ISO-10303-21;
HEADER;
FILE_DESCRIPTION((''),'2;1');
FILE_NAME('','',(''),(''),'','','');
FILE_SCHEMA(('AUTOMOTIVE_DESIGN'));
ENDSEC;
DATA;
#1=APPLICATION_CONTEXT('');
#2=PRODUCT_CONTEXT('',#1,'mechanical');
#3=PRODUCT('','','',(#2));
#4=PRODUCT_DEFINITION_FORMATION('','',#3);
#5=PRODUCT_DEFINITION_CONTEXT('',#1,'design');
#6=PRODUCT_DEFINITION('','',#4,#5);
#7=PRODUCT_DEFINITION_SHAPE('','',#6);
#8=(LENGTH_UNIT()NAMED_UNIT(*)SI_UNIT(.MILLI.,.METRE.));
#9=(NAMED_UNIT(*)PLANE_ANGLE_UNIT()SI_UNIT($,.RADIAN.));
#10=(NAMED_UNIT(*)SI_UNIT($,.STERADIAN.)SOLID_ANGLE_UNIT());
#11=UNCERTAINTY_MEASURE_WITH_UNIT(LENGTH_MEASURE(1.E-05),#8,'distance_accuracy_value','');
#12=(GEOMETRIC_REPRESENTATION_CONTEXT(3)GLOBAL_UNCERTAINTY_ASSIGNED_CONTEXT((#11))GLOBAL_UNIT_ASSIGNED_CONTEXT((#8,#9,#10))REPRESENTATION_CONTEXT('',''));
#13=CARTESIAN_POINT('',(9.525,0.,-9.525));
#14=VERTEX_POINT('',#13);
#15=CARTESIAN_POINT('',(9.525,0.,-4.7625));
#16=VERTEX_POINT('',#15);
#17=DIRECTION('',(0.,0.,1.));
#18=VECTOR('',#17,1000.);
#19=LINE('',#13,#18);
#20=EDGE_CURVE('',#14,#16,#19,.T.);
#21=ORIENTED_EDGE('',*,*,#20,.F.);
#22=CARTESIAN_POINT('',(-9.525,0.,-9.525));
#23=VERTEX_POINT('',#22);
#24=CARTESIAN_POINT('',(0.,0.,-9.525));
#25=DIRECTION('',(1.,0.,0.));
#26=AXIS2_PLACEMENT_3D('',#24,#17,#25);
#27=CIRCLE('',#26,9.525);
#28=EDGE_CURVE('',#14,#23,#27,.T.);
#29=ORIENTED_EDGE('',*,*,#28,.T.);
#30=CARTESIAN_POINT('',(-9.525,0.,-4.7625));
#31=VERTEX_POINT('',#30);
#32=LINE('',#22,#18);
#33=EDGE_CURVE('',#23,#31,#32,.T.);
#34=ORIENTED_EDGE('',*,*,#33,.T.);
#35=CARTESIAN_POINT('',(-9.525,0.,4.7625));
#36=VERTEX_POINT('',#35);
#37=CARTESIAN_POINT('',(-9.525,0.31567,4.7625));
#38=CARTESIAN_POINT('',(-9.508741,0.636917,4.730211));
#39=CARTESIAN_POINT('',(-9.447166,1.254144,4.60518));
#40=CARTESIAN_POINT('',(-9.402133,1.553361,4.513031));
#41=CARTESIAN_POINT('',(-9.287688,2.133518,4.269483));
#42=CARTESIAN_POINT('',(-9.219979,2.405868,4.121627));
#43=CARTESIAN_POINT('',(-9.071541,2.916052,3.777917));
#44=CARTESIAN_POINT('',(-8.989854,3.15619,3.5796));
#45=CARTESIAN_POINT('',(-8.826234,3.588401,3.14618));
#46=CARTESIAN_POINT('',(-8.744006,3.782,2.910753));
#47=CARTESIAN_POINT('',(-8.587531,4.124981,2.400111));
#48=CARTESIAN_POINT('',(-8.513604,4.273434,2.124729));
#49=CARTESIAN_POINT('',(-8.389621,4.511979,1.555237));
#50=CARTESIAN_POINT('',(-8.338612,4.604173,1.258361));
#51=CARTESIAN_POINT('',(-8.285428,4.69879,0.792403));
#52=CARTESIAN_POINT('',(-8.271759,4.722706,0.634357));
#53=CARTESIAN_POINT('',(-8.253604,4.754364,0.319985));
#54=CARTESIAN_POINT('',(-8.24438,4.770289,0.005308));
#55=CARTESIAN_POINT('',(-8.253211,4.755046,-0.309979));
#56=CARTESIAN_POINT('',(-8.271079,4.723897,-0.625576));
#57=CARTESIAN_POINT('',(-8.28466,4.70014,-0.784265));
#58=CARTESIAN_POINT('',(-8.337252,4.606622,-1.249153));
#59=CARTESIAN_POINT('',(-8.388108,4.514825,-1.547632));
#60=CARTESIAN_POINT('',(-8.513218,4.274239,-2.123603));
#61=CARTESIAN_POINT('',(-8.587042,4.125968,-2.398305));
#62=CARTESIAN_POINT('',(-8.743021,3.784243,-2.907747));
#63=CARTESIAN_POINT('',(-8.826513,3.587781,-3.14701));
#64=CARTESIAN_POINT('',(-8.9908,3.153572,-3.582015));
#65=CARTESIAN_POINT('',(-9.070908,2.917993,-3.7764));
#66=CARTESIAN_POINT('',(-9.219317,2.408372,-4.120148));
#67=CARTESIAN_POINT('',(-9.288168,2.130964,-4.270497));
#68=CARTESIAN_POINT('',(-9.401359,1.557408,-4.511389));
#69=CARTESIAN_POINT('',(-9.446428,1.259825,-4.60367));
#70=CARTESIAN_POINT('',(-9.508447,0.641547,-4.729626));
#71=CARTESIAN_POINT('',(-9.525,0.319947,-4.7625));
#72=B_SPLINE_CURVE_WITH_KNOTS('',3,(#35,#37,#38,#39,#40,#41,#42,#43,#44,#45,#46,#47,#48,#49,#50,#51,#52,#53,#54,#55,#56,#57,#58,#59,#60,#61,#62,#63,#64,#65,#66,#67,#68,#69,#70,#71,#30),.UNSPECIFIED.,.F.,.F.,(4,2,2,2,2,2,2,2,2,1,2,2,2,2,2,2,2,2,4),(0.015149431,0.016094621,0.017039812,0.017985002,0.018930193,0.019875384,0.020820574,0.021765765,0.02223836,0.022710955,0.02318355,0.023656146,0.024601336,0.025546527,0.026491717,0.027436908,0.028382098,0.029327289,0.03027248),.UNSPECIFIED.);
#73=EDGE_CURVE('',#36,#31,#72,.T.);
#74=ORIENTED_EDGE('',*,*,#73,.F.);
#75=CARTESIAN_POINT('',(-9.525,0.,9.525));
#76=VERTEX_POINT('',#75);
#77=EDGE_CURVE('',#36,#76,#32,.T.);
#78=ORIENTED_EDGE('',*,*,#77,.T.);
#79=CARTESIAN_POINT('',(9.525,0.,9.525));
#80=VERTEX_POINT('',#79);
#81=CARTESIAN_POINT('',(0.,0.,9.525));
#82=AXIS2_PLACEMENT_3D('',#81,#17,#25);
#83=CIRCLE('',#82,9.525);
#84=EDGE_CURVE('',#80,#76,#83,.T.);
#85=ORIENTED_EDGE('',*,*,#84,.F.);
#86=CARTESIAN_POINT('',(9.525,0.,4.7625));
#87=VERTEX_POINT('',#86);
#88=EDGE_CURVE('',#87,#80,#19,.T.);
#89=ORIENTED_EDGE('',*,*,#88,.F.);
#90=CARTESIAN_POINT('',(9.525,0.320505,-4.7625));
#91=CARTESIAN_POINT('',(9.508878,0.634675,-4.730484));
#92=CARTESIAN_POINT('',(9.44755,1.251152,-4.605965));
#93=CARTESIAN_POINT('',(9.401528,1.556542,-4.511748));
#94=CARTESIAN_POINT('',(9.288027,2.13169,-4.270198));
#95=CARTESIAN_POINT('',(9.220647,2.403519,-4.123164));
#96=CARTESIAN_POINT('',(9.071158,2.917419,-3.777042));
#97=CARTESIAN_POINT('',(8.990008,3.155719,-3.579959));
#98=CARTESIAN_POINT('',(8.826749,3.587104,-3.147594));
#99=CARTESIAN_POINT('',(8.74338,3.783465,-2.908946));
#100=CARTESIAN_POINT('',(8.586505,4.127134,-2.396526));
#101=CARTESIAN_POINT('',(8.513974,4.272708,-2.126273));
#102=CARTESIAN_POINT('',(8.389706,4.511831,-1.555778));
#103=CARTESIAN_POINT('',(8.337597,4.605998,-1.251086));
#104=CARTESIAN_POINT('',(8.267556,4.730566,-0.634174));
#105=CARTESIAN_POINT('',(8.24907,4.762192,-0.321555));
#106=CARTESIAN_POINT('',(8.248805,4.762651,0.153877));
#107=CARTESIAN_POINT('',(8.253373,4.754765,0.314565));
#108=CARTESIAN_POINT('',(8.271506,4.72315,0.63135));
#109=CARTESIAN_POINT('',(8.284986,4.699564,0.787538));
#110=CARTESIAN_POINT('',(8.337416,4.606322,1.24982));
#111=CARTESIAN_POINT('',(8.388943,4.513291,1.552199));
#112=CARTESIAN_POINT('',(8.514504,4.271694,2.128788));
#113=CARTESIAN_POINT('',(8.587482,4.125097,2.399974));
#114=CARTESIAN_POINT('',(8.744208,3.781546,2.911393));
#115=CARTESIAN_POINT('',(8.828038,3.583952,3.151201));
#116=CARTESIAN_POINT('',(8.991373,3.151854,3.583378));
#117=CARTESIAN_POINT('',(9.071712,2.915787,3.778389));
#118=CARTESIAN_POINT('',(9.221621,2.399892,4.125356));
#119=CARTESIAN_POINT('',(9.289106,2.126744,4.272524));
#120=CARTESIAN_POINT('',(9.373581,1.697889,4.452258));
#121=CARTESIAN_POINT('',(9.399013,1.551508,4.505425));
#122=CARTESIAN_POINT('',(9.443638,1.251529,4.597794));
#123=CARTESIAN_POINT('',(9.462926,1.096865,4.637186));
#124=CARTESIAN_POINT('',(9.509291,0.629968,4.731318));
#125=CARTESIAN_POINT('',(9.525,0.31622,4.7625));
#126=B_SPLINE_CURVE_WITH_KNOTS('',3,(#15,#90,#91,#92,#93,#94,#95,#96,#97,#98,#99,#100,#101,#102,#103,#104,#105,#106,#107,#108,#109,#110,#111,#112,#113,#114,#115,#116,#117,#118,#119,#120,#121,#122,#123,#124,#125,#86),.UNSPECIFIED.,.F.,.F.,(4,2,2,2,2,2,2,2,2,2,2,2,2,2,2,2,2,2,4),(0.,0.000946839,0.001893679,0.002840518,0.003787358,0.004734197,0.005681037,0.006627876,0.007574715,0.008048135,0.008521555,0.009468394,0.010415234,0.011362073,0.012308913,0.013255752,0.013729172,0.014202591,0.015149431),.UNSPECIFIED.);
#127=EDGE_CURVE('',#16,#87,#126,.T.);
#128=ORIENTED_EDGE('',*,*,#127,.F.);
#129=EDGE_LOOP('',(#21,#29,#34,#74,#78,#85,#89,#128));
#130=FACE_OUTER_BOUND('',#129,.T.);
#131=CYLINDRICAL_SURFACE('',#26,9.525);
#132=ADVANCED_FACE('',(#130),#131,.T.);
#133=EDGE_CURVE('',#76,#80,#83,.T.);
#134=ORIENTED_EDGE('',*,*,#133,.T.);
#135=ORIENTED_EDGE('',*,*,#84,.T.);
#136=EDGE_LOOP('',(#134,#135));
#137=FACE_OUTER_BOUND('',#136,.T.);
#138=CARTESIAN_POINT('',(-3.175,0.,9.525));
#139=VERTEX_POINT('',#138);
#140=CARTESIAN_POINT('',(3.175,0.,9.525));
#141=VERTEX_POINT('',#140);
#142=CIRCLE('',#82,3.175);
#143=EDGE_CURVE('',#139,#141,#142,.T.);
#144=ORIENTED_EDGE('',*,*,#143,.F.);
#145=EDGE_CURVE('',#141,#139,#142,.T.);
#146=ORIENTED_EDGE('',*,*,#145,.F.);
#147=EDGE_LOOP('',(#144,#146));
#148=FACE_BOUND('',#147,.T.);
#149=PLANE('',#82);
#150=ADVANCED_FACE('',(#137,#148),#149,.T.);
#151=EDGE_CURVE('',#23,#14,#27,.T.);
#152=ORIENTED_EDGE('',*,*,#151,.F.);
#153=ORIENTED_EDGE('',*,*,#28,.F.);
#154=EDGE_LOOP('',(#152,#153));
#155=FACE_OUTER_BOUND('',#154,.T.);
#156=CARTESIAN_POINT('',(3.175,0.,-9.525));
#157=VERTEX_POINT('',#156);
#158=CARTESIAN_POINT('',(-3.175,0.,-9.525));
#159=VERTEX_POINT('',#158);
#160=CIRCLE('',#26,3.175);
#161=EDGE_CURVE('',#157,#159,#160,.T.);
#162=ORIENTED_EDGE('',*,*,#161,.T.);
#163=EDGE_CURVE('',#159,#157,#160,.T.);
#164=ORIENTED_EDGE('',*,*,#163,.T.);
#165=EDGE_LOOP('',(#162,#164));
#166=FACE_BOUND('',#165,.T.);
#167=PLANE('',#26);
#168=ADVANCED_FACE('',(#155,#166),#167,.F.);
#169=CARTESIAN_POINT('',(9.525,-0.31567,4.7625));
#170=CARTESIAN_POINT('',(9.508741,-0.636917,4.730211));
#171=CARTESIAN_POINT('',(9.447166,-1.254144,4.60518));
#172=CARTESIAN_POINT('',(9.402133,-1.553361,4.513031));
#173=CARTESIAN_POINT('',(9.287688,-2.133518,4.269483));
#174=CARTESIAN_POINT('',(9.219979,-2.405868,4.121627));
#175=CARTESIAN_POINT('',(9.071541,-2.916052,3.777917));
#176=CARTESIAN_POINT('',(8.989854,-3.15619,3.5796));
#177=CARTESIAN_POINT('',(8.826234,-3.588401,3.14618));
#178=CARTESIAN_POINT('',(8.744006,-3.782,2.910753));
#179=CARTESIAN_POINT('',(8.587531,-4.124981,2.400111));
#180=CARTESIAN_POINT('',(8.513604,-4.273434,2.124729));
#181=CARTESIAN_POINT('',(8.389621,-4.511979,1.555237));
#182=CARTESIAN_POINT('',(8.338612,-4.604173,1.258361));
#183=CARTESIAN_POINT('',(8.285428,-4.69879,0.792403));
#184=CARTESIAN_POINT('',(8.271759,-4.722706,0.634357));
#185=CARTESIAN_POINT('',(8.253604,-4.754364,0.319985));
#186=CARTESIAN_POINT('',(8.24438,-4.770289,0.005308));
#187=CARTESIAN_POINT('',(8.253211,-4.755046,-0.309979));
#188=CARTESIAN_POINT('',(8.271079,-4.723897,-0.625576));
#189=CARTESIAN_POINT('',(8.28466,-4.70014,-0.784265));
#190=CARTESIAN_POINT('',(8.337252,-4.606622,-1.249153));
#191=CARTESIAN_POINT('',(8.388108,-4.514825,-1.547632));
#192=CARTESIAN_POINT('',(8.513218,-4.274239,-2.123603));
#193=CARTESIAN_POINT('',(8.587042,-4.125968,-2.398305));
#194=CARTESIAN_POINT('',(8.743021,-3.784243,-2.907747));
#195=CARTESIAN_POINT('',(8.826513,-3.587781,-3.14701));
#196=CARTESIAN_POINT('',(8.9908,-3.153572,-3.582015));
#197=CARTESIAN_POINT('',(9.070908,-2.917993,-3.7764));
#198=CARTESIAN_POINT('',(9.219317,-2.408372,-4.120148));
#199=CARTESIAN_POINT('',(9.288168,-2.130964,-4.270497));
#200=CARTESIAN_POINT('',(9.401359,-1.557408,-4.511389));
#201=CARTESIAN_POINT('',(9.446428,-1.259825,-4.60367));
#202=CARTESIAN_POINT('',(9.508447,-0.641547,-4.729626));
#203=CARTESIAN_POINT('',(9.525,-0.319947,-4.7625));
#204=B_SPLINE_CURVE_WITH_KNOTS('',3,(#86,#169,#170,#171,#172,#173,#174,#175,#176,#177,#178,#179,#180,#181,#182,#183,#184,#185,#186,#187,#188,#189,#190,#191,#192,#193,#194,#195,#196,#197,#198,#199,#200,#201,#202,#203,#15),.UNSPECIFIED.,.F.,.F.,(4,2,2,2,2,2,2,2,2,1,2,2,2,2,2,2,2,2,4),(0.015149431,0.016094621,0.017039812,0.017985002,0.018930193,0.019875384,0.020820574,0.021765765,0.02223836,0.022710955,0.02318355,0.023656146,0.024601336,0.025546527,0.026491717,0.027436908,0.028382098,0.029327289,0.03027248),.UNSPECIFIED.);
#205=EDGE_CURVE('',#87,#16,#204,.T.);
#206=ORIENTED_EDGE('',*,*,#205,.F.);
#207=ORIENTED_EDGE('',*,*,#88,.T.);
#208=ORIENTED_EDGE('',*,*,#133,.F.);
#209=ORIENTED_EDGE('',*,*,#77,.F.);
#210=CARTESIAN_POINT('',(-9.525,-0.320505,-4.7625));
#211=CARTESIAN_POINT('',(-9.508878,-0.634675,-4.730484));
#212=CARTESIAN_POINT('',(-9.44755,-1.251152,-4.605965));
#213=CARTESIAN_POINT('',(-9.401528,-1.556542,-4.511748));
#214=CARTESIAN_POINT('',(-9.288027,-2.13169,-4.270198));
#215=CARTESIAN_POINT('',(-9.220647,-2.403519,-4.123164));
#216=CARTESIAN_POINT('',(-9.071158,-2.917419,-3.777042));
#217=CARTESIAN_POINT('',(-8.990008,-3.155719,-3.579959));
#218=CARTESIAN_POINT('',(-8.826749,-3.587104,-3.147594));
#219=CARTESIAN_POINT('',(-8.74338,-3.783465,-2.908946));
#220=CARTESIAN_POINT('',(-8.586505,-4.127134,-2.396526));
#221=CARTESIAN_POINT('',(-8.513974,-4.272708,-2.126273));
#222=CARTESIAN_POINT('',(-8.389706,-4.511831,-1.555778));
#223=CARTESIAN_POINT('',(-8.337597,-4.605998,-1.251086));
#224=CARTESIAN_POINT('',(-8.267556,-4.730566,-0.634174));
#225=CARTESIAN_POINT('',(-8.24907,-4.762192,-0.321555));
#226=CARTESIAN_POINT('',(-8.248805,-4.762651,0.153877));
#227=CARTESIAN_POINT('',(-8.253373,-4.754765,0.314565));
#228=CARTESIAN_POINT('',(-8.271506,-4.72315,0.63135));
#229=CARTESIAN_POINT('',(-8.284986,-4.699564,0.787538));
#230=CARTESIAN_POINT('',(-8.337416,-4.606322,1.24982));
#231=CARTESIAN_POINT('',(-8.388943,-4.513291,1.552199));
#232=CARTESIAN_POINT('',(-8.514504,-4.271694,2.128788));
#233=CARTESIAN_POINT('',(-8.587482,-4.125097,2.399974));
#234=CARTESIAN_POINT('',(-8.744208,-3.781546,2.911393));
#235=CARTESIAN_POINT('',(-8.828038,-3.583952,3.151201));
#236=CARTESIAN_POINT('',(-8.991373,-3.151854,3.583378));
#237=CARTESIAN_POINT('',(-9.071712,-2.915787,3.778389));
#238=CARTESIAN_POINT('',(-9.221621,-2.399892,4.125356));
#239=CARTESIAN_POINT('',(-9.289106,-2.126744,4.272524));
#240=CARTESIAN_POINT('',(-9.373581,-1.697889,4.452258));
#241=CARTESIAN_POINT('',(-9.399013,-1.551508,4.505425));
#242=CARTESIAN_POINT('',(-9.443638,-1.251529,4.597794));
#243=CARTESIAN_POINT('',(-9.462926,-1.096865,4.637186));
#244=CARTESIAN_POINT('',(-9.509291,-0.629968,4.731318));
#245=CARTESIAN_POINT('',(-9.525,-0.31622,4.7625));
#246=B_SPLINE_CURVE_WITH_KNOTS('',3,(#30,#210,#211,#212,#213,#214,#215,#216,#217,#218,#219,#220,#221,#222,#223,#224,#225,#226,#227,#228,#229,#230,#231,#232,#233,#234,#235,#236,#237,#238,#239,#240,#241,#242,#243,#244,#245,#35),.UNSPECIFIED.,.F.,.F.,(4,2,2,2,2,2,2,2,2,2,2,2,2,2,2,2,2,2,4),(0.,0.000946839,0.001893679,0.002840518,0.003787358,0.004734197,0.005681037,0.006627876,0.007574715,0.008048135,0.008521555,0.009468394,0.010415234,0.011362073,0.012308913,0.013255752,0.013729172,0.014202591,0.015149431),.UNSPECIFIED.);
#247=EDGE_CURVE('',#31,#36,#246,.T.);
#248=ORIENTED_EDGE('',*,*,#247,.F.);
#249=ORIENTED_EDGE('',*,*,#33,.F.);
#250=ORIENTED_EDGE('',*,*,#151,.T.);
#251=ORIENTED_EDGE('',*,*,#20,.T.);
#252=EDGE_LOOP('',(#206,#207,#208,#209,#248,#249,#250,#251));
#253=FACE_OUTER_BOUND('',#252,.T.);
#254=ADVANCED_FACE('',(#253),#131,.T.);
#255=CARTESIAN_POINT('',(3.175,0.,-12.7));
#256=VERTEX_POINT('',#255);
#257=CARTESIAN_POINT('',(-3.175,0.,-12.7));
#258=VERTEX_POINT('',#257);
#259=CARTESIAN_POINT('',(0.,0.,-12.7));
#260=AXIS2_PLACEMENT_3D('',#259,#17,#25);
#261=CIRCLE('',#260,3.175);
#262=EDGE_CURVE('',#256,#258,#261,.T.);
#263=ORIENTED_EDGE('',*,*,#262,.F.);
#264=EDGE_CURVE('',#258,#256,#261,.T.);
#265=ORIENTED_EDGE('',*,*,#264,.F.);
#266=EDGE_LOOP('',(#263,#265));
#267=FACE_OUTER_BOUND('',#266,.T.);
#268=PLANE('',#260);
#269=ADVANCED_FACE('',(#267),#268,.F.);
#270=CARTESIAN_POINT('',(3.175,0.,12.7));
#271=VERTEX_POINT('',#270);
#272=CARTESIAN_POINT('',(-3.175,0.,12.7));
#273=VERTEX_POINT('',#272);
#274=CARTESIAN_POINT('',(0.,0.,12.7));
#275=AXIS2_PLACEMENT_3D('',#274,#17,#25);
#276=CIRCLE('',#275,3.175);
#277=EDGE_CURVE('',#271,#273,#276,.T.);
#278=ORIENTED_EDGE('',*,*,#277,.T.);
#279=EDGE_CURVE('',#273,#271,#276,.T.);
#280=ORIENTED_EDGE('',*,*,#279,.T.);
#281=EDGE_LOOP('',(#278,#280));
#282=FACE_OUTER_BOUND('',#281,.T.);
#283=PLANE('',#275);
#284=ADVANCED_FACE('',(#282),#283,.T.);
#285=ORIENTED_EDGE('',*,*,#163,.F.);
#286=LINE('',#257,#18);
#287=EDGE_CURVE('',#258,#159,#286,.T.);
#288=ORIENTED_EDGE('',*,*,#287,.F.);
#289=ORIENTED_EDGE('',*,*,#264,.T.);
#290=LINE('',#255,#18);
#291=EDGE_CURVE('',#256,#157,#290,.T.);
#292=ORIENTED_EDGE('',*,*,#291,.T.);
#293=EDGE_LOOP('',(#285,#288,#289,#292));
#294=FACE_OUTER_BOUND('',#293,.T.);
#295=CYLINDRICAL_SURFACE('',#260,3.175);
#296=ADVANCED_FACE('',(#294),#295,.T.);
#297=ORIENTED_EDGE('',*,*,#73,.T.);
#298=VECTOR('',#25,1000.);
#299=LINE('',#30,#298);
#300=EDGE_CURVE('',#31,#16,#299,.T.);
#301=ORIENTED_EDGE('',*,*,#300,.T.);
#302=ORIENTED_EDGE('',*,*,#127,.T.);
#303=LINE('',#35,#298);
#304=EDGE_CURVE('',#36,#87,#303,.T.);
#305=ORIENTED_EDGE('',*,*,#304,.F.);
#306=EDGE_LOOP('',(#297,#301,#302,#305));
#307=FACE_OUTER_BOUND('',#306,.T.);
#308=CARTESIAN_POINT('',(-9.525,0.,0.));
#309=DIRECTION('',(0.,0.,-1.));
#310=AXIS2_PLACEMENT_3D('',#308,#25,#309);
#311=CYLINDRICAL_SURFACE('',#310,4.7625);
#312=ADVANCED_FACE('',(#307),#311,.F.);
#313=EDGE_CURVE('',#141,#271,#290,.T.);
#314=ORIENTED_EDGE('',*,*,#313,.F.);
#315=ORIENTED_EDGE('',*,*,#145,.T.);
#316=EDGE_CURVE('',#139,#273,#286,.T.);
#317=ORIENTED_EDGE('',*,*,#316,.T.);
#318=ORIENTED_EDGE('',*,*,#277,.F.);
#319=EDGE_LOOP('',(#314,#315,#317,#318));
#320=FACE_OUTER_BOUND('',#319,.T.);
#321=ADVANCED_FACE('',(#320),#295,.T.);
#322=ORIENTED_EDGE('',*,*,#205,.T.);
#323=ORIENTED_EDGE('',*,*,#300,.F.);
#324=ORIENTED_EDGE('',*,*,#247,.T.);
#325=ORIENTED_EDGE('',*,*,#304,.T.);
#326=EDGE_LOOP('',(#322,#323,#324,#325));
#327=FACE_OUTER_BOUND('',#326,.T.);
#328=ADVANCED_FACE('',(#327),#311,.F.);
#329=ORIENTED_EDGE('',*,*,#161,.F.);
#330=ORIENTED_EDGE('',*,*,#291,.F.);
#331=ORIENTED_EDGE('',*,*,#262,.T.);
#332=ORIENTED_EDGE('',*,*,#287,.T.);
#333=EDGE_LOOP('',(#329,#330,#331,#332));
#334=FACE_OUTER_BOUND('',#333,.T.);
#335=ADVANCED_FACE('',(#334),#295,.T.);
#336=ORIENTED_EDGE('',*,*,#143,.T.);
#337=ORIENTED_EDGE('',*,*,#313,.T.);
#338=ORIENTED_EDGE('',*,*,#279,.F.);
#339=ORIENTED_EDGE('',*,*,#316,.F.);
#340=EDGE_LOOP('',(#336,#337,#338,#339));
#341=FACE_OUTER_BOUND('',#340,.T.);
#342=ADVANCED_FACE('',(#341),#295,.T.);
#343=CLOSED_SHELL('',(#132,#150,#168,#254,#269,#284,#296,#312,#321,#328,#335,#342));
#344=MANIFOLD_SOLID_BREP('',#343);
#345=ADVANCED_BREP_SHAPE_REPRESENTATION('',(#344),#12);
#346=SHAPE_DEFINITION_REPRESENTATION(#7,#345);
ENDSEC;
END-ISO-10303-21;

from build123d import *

# Parameters (mm, degrees)
BOSS_EXTRUDE1_DEPTH      = 9.525
BOSS_EXTRUDE1_DEPTH_BACK = 9.525
SKETCH1_R                = 9.525
BOSS_EXTRUDE2_DEPTH      = 12.7
BOSS_EXTRUDE2_DEPTH_BACK = 12.7
BOSS_EXTRUDE2_START      = -9.525
SKETCH2_R                = 3.175
CUT_EXTRUDE1_DEPTH       = 19.513272266
CUT_EXTRUDE1_DEPTH_BACK  = 19.513272266
SKETCH3_R                = 4.7625


with BuildPart() as part:
    # Sketch1 → Boss-Extrude1 (new, two sides: drawn at the far end of the back side and taken through both)
    with BuildSketch(Plane.XY.offset(-BOSS_EXTRUDE1_DEPTH_BACK)):
        Circle(SKETCH1_R)
    extrude(amount=BOSS_EXTRUDE1_DEPTH + BOSS_EXTRUDE1_DEPTH_BACK)

    # Sketch2 → Boss-Extrude2 (add, two sides: drawn at the far end of the back side and taken through both)
    with BuildSketch(Plane.XY.offset(9.525).offset(BOSS_EXTRUDE2_START - BOSS_EXTRUDE2_DEPTH_BACK)):
        Circle(SKETCH2_R)
    extrude(amount=BOSS_EXTRUDE2_DEPTH + BOSS_EXTRUDE2_DEPTH_BACK)

    # Sketch3 → Cut-Extrude1 (cut, two sides: drawn at the far end of the back side and taken through both)
    with BuildSketch(Plane(origin=(0, 0, 0), x_dir=(0, 0, -1), z_dir=(1, 0, 0)).offset(-CUT_EXTRUDE1_DEPTH_BACK)):
        Circle(SKETCH3_R)
    extrude(amount=CUT_EXTRUDE1_DEPTH + CUT_EXTRUDE1_DEPTH_BACK, mode=Mode.SUBTRACT)


solid = part.part
